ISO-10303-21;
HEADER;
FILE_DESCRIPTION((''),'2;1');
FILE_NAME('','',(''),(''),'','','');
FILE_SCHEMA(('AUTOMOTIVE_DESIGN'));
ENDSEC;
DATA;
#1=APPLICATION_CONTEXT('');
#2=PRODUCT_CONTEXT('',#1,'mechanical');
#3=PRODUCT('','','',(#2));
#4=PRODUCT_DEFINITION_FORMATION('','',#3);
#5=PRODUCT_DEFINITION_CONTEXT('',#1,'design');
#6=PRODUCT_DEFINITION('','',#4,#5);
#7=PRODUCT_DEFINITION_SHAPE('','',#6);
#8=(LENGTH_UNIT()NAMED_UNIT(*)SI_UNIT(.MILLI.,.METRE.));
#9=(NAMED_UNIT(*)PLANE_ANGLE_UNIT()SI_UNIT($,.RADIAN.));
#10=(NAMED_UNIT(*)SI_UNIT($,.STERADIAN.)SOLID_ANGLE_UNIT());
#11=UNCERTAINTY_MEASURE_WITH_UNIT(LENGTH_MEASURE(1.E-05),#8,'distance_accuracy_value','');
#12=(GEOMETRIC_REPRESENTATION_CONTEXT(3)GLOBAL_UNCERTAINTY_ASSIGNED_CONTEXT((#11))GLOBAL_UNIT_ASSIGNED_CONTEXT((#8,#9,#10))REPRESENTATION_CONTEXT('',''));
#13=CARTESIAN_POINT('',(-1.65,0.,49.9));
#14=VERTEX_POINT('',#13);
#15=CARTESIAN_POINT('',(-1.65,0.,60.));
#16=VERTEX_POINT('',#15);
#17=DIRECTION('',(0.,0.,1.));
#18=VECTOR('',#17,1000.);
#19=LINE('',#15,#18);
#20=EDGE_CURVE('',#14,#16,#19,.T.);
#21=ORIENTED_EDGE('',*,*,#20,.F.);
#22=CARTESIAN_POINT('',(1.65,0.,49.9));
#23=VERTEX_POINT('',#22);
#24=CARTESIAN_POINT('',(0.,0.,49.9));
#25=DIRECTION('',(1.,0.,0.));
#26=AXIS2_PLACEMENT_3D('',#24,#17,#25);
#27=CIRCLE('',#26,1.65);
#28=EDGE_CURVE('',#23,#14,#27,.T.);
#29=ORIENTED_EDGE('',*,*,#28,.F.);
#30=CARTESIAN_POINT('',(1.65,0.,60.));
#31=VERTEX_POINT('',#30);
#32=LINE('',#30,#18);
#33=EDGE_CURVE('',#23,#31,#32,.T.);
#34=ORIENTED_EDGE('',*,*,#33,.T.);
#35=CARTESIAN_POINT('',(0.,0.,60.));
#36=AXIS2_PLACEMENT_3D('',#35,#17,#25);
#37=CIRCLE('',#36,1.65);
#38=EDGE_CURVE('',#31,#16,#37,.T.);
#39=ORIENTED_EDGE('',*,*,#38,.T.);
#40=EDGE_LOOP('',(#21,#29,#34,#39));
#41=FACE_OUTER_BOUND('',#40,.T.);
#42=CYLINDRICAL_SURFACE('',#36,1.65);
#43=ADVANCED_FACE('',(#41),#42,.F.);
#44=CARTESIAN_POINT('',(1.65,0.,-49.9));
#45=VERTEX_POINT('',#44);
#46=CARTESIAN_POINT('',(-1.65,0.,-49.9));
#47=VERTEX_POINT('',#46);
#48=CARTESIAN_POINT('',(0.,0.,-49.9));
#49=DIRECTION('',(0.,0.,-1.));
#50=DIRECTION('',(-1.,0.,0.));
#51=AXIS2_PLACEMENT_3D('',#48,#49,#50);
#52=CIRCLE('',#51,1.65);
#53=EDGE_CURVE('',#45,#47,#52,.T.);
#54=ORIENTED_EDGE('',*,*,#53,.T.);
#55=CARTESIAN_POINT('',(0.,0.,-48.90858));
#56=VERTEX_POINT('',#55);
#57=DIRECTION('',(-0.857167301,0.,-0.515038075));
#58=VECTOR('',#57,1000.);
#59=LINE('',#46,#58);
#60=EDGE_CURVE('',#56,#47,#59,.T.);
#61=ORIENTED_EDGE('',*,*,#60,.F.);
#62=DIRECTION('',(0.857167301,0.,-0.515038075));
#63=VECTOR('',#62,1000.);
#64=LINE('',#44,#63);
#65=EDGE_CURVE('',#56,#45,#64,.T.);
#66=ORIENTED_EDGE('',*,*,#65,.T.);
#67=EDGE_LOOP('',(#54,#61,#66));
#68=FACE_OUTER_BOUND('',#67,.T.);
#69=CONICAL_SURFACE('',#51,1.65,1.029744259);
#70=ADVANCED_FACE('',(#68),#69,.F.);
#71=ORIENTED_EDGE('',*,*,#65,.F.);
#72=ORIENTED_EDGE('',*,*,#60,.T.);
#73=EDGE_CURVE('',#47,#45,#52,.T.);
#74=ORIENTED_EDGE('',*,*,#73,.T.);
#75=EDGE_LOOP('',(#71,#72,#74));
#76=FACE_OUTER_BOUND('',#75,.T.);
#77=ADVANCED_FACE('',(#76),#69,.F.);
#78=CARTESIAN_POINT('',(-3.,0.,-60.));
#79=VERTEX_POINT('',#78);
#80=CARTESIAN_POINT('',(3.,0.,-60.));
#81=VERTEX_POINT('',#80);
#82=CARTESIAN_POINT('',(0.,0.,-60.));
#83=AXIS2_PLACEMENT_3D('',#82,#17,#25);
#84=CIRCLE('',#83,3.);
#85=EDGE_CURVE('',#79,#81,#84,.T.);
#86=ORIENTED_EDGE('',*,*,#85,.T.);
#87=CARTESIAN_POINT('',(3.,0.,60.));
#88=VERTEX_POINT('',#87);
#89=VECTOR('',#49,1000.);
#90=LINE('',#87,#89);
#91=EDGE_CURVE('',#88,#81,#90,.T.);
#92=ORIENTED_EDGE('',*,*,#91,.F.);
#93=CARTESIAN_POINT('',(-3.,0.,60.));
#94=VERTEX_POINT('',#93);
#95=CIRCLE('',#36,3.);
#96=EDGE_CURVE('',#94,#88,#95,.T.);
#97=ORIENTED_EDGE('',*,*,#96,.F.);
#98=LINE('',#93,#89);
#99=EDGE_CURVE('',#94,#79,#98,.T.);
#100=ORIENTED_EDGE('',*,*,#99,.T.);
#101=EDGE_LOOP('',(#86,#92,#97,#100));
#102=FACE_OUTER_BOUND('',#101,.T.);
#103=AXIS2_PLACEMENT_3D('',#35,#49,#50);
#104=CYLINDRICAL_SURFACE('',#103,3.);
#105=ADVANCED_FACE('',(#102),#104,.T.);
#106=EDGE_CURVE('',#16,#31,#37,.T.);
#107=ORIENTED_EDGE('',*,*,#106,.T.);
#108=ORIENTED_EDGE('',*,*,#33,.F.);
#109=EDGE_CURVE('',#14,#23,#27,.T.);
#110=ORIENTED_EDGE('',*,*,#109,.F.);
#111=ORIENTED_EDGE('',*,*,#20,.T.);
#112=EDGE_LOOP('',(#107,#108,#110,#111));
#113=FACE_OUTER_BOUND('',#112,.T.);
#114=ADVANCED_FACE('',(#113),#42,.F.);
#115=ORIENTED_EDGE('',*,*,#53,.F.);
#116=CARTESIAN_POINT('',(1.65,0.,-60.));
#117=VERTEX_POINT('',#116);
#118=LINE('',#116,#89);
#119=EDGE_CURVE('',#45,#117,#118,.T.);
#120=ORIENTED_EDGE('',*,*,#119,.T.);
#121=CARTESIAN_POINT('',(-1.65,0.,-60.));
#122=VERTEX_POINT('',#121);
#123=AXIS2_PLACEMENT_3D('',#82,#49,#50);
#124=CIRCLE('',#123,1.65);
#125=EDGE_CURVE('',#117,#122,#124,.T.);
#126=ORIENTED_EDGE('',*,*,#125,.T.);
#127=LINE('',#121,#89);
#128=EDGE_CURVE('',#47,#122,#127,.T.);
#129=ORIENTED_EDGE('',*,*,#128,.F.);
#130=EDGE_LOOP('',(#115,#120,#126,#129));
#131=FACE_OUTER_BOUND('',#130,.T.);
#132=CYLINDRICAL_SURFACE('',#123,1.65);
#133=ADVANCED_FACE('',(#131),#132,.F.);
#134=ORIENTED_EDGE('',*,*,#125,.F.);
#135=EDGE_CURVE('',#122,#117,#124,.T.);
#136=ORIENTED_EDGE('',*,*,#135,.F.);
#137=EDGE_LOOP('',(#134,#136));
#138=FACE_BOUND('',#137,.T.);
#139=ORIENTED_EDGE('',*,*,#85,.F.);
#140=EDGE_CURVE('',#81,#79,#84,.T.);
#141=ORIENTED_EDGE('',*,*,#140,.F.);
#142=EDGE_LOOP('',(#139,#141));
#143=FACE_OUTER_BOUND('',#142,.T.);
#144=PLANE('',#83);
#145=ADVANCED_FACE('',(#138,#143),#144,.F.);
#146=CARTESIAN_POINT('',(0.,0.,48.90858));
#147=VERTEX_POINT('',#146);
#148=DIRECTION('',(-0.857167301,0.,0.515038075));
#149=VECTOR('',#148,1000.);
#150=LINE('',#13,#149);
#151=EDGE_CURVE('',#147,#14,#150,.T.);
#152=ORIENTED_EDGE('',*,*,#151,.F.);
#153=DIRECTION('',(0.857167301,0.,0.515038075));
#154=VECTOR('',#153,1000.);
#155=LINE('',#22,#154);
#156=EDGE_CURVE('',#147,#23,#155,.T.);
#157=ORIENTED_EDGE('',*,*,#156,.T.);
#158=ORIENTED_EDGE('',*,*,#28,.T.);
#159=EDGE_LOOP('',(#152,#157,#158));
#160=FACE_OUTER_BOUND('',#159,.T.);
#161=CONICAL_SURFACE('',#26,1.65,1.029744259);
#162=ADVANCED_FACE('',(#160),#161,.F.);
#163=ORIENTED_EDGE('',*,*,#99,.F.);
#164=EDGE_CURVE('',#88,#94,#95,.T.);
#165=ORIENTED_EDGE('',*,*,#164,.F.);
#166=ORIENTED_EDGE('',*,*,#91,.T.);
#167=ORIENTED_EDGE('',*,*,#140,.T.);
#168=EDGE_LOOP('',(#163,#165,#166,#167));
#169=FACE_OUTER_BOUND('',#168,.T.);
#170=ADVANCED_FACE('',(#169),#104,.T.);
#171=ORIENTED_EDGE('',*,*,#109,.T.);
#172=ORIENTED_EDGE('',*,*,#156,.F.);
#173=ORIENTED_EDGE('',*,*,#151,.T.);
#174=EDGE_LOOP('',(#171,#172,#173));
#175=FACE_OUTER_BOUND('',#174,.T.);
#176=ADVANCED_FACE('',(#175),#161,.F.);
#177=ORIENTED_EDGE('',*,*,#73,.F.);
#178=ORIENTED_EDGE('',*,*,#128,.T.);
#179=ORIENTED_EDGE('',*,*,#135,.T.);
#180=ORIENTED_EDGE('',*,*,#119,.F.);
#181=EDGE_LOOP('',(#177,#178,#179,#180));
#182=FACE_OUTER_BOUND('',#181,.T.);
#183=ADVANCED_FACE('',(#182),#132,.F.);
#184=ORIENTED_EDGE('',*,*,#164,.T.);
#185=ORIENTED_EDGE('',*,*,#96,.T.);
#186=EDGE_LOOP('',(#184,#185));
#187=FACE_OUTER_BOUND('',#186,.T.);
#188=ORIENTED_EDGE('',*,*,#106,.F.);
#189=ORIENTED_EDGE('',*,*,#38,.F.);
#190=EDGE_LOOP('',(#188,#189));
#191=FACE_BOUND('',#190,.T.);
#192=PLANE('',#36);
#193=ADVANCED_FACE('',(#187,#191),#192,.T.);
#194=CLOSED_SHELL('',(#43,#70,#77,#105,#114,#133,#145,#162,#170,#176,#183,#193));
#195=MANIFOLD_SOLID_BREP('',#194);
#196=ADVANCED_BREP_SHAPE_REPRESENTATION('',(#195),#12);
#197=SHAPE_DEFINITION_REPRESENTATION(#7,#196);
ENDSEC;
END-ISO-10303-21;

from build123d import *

# Parameters (mm, degrees)
SKETCH1_R             = 3
BOSS_EXTRUDE1_DEPTH   = 60
M4_TAPPED_HOLE1_D     = 3.3
M4_TAPPED_HOLE1_DEPTH = 10.1
M4_TAPPED_HOLE1_TIP   = 0.991420021
M4_TAPPED_HOLE2_D     = 3.3
M4_TAPPED_HOLE2_DEPTH = 10.1
M4_TAPPED_HOLE2_TIP   = 0.991420021


with BuildPart() as part:
    # Sketch1 → Boss-Extrude1 (new, symmetric)
    with BuildSketch(Plane.XY):
        Circle(SKETCH1_R)
    extrude(amount=BOSS_EXTRUDE1_DEPTH, both=True)

    # M4 Tapped Hole1
    with Locations(Plane.XY.offset(60)):
        with Locations((0, 0)):
            Hole(M4_TAPPED_HOLE1_D / 2, depth=M4_TAPPED_HOLE1_DEPTH)
            with Locations((0, 0, -(M4_TAPPED_HOLE1_DEPTH + M4_TAPPED_HOLE1_TIP / 2))):  # 118° drill point
                Cone(0, M4_TAPPED_HOLE1_D / 2, M4_TAPPED_HOLE1_TIP, mode=Mode.SUBTRACT)

    # M4 Tapped Hole2
    with Locations(Plane(origin=(0, 0, -60), x_dir=(-1, 0, 0), z_dir=(0, 0, -1))):
        with Locations((0, 0)):
            Hole(M4_TAPPED_HOLE2_D / 2, depth=M4_TAPPED_HOLE2_DEPTH)
            with Locations((0, 0, -(M4_TAPPED_HOLE2_DEPTH + M4_TAPPED_HOLE2_TIP / 2))):  # 118° drill point
                Cone(0, M4_TAPPED_HOLE2_D / 2, M4_TAPPED_HOLE2_TIP, mode=Mode.SUBTRACT)


solid = part.part
